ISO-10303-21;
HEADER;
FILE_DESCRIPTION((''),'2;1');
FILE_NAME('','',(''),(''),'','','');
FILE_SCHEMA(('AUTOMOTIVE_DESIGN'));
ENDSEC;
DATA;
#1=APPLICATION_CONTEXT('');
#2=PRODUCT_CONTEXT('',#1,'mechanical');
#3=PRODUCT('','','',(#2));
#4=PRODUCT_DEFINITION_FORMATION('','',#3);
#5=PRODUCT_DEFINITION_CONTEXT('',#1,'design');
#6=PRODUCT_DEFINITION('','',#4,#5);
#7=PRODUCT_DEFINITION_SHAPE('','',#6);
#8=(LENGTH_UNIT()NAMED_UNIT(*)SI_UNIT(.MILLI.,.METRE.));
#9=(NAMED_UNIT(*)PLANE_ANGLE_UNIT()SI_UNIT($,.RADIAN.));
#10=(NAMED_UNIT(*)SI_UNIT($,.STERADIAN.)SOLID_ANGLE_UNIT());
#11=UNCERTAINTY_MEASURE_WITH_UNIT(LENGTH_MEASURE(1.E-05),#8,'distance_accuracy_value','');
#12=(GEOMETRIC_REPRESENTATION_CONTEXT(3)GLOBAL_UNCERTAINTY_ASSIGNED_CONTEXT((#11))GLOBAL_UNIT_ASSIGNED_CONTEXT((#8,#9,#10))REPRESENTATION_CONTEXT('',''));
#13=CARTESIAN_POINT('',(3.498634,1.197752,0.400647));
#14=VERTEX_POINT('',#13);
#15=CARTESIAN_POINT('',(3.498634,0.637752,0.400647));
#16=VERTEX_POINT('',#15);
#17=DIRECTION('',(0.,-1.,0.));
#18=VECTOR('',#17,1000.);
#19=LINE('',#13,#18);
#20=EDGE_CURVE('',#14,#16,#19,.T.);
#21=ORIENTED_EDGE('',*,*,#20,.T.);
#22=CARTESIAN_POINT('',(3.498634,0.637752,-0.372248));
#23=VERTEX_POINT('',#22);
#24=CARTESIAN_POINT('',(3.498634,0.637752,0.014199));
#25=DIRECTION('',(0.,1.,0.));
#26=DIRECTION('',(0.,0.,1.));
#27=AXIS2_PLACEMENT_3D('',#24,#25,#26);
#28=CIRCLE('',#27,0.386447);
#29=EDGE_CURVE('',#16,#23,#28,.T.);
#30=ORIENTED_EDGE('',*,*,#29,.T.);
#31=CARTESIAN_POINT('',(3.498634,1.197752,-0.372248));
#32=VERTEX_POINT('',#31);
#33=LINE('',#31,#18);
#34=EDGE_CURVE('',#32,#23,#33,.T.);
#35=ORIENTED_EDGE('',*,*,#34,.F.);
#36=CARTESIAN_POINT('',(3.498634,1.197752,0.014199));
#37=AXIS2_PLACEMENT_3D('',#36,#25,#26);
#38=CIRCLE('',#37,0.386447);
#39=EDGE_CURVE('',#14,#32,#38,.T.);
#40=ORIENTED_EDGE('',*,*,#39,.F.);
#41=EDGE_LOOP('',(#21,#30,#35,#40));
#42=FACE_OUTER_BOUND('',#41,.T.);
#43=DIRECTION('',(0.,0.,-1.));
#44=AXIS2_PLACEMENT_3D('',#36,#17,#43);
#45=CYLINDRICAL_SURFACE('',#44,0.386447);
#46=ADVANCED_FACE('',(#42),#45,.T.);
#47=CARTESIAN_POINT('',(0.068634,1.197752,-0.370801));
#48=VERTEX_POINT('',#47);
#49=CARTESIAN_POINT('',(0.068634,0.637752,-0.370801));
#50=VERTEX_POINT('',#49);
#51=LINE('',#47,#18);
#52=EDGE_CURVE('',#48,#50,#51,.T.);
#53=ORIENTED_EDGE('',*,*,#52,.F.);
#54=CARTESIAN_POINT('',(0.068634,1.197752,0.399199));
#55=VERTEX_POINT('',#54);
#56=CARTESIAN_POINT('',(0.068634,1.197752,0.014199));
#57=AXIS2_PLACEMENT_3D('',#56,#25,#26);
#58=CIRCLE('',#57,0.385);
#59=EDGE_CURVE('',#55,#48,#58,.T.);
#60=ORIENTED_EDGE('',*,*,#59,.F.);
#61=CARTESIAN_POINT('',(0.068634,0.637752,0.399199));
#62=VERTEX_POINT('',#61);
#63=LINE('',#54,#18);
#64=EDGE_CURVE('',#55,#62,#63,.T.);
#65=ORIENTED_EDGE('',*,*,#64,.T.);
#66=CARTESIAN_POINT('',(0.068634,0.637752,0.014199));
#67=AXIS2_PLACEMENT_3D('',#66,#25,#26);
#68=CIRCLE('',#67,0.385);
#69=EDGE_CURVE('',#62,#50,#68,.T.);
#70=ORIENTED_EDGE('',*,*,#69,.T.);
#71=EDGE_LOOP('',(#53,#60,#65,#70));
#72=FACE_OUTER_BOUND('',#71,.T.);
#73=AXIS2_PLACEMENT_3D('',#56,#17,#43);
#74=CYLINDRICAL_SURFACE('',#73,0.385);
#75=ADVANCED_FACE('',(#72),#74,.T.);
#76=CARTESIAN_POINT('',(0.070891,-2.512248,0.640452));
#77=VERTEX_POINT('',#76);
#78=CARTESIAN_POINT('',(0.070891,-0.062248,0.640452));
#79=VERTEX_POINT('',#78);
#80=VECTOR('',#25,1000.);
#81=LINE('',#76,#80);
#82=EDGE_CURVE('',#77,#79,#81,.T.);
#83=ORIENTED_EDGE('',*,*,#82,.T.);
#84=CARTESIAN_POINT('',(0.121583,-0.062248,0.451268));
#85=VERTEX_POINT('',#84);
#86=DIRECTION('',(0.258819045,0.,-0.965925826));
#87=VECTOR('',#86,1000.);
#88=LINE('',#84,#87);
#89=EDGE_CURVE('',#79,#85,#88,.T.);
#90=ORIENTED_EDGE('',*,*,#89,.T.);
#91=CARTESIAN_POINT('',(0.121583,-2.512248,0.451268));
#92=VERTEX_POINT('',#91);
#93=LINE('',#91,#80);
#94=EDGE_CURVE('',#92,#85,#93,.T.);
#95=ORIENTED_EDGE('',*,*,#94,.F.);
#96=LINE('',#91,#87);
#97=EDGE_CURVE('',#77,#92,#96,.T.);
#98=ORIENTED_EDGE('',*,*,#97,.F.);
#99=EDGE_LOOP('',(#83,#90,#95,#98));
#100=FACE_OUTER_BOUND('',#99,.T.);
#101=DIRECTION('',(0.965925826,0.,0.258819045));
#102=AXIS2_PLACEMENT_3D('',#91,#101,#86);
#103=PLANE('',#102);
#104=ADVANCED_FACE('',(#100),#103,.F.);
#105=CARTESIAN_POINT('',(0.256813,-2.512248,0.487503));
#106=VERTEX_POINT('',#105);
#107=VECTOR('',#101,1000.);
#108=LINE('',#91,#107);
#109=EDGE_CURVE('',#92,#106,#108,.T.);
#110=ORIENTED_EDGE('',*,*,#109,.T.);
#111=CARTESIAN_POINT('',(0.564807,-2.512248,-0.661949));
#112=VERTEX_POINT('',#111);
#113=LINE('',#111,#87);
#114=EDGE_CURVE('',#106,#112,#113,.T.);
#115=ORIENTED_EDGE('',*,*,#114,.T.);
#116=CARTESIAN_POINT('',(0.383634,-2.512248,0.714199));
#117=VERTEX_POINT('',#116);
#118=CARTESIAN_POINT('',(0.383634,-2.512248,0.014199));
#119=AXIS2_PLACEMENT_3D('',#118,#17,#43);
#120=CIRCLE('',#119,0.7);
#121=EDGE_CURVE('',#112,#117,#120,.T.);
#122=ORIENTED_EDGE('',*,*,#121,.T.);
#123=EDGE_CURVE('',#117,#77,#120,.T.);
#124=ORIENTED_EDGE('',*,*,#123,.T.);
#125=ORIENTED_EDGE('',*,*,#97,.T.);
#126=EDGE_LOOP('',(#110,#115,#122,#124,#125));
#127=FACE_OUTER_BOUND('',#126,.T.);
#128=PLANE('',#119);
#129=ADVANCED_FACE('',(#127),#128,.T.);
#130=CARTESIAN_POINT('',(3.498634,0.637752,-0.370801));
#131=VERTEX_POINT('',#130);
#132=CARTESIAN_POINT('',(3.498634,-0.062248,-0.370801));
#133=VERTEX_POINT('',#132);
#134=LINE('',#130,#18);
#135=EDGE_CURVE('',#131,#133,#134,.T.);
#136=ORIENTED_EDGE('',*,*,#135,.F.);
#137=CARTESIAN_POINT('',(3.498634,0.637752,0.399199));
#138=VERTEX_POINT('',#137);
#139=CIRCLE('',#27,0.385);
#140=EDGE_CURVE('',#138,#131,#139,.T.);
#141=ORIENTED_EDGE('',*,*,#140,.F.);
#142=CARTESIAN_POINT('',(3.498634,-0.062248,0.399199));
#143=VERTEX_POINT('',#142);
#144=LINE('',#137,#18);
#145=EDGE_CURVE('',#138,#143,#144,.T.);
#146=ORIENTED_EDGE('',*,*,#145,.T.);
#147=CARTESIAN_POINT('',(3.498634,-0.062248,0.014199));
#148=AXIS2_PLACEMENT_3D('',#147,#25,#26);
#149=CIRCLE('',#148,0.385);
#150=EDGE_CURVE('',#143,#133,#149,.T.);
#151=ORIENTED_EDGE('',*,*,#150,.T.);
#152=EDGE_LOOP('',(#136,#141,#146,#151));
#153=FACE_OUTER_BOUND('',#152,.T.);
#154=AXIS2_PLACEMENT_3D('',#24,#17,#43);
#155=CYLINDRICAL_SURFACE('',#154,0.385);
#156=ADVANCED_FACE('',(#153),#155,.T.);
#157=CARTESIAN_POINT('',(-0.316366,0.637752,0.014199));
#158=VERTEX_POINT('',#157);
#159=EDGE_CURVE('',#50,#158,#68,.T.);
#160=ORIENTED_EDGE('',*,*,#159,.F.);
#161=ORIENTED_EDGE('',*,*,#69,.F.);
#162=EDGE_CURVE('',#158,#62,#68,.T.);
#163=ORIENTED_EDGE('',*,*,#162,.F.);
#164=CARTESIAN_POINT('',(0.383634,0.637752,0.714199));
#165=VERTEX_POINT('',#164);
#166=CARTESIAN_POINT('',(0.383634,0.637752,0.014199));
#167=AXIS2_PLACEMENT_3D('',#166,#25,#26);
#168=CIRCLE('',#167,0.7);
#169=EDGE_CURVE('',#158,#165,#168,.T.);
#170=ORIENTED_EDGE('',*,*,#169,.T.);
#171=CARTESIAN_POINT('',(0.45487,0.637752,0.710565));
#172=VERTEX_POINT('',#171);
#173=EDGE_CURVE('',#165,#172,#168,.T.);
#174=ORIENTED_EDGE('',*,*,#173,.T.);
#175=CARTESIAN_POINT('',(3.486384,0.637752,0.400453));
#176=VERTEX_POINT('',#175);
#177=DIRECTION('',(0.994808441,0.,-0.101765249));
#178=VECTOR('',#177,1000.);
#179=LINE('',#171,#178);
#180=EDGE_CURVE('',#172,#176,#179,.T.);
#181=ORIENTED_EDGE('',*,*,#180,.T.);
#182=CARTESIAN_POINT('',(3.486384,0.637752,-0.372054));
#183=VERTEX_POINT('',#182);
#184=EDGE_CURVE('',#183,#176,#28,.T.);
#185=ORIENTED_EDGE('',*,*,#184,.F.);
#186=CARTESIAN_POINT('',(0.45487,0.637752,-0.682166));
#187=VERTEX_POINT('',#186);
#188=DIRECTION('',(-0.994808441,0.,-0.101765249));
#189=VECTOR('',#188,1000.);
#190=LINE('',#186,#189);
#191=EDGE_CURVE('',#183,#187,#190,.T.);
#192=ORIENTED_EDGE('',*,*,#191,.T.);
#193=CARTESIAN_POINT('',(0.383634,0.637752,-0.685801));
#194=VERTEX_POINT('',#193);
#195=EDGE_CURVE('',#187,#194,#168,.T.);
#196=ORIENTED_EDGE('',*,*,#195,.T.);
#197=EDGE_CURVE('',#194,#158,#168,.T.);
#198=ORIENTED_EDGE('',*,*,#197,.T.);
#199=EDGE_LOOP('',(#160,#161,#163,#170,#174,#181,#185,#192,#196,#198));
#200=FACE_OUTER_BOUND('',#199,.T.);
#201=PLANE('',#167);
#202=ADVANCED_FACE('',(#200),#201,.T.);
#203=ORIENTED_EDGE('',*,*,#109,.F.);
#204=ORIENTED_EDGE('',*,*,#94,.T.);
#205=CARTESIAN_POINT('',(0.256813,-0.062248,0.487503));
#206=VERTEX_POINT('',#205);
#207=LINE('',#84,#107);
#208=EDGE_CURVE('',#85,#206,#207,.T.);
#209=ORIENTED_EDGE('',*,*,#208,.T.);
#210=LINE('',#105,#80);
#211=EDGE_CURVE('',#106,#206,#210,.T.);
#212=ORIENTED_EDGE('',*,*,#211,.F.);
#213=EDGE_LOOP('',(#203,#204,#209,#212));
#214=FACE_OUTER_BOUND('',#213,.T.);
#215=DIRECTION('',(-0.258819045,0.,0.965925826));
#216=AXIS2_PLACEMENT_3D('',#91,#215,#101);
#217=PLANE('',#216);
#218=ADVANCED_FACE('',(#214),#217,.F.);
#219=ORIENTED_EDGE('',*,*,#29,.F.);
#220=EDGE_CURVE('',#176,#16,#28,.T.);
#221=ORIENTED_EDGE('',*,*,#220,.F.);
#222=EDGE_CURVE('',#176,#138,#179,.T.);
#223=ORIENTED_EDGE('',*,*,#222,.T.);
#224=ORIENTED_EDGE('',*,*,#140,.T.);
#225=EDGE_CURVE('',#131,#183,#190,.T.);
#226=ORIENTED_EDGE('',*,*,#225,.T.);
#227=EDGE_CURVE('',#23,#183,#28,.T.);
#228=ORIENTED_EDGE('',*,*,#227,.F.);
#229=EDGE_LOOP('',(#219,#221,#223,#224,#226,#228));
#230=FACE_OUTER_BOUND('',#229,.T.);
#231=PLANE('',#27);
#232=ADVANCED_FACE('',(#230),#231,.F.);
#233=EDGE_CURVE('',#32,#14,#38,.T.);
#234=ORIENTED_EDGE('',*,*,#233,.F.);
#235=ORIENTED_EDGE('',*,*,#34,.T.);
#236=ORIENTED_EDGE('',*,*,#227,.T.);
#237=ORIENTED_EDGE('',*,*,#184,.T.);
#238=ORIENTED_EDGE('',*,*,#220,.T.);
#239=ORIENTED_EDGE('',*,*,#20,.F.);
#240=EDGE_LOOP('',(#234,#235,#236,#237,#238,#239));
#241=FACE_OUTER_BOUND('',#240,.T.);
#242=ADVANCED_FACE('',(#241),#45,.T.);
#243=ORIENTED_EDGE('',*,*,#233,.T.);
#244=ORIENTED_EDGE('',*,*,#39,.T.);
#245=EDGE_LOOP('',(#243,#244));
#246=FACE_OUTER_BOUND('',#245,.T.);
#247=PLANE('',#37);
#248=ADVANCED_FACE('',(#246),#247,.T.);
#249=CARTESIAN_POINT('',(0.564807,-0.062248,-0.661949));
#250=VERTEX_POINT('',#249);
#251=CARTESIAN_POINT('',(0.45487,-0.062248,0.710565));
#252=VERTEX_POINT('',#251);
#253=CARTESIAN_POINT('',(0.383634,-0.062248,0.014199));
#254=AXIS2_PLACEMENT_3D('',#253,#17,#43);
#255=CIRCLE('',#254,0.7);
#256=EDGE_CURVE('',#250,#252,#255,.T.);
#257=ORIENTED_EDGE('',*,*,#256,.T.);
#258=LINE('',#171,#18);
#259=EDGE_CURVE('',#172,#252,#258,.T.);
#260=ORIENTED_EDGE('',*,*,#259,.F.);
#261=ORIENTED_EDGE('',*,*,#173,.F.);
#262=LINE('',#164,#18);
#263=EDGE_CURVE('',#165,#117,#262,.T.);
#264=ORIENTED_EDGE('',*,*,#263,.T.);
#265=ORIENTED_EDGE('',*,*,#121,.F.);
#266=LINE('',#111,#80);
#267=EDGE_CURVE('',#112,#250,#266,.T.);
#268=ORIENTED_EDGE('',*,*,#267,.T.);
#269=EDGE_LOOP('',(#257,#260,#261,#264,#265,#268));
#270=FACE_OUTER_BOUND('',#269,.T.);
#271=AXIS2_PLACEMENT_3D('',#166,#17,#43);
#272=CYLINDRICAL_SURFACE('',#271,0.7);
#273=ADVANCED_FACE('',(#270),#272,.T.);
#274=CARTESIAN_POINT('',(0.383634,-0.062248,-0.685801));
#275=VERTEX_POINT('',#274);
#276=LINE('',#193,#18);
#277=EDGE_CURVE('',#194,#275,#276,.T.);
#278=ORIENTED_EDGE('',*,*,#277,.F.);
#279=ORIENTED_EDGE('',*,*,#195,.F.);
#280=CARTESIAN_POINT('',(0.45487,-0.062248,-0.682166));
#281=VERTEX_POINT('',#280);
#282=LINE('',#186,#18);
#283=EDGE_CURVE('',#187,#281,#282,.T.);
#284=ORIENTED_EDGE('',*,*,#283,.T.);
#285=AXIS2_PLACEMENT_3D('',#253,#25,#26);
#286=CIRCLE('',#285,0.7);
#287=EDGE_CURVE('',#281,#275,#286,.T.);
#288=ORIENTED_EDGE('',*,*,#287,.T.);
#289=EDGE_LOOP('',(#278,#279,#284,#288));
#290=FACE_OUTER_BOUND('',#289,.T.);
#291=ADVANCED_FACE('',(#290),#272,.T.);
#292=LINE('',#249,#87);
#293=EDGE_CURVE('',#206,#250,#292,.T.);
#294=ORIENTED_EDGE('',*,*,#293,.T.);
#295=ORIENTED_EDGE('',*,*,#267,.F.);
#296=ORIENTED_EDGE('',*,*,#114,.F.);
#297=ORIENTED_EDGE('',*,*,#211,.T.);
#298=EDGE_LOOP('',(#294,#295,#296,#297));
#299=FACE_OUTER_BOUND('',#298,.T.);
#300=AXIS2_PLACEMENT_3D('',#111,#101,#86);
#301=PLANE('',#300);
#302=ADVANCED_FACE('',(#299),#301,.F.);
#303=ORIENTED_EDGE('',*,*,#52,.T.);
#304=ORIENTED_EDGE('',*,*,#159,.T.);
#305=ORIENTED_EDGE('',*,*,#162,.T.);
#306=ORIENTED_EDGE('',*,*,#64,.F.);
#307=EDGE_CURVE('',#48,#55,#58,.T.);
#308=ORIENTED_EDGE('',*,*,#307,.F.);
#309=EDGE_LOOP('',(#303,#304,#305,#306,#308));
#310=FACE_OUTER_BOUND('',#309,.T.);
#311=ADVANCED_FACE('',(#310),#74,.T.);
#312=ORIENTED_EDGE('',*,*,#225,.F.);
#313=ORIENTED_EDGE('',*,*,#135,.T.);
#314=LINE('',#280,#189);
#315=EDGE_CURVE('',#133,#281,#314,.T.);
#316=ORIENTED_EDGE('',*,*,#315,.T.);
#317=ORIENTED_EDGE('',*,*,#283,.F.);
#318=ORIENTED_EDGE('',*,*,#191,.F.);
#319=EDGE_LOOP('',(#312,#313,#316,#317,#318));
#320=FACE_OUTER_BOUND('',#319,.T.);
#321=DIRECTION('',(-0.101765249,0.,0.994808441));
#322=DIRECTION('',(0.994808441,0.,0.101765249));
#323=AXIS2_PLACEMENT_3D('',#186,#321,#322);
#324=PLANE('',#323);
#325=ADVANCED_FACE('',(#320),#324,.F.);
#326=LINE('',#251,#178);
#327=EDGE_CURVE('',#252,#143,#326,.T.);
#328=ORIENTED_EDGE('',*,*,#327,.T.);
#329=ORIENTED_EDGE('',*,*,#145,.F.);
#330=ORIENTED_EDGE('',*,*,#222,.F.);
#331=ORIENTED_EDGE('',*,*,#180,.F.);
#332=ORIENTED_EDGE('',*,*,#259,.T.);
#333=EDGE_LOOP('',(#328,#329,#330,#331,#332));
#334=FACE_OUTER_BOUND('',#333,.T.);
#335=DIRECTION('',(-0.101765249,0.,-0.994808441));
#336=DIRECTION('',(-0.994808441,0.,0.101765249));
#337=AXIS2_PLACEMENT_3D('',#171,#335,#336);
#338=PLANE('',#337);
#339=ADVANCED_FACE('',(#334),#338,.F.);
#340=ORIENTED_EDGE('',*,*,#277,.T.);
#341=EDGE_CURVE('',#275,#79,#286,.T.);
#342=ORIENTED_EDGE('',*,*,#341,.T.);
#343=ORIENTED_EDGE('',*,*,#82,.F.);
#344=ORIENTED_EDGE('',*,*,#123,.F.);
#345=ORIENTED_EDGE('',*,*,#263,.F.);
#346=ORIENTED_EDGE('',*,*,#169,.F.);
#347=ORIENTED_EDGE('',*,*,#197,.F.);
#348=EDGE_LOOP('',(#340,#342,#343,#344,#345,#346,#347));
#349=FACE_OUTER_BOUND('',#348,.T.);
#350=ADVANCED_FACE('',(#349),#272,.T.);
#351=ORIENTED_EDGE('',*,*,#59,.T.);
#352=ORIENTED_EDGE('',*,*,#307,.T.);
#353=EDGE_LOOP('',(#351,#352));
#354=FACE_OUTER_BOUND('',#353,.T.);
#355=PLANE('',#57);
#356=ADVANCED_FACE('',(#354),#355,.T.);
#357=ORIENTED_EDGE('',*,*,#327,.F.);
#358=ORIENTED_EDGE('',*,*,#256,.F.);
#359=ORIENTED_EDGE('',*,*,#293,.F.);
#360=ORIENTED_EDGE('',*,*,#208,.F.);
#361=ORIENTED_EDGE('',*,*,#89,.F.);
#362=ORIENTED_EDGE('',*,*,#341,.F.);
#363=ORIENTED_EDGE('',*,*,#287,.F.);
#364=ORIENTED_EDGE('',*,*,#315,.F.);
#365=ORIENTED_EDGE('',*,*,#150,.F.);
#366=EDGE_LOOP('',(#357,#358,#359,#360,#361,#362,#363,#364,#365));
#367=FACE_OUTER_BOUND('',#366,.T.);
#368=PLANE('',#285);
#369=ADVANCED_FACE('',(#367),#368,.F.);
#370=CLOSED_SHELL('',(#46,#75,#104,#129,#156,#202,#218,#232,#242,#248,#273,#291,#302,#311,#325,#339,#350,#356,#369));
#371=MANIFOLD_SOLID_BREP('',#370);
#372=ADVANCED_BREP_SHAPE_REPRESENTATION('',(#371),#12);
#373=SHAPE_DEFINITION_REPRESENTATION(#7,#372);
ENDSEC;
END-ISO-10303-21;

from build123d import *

# Parameters (mm, degrees)
EXTRUDE_1_DEPTH = 1
SKETCH_2_R      = 0.552067548
SKETCH_2_R_2    = 0.55
EXTRUDE_2_DEPTH = 0.8
EXTRUDE_START   = 3.5
EXTRUDE_3_DEPTH = 3.5
SCALE_1_SCALE   = 0.7


with BuildPart() as part:
    # 草图1 → 凸台-拉伸1 (new body)
    with BuildSketch(Plane(origin=(0, 0, 0), x_dir=(1, 0, 0), z_dir=(0, 1, 0))):
        with BuildLine():
            Line((0.101765249, -0.994808441), (4.45, -0.55))
            ThreePointArc((4.45, -0.55), (5, 0), (4.45, 0.55))
            Line((4.45, 0.55), (0.101765249, 0.994808441))
            ThreePointArc((0.101765249, 0.994808441), (-1, 0), (0.101765249, -0.994808441))
        make_face()
    extrude(amount=EXTRUDE_1_DEPTH)

    # 草图2 → 凸台-拉伸2 (add)
    with BuildSketch(Plane(origin=(0, 1, 0), x_dir=(1, 0, 0), z_dir=(0, 1, 0))):
        with Locations(Location((4.45, 0, 0), (0, 0, 91.816467299))):
            Circle(SKETCH_2_R)
        with Locations(Location((-0.45, 0, 0), (0, 0, 179.998371267))):
            Circle(SKETCH_2_R_2)
    extrude(amount=EXTRUDE_2_DEPTH)

    # 草图3 → 凸台-拉伸3 (add)
    with BuildSketch(Plane.XZ.offset(EXTRUDE_START)):
        with BuildLine():
            Line((0.258819045, -0.965925826), (-0.181173332, 0.676148078))
            Line((-0.181173332, 0.676148078), (-0.374358497, 0.624384269))
            Line((-0.374358497, 0.624384269), (-0.446775004, 0.894646352))
            ThreePointArc((-0.446775004, 0.894646352), (0.935020892, 0.354592627), (0.258819045, -0.965925826))
        make_face()
    extrude(amount=-EXTRUDE_3_DEPTH)


with BuildPart() as part_1:
    # 缩放比例1: scaled about (1.278779504, -0.207492691, 0.047331659)
    add(part.part.scale(SCALE_1_SCALE).moved(Location((0.383633851, -0.062247807, 0.014199498))))


solid = part_1.part
